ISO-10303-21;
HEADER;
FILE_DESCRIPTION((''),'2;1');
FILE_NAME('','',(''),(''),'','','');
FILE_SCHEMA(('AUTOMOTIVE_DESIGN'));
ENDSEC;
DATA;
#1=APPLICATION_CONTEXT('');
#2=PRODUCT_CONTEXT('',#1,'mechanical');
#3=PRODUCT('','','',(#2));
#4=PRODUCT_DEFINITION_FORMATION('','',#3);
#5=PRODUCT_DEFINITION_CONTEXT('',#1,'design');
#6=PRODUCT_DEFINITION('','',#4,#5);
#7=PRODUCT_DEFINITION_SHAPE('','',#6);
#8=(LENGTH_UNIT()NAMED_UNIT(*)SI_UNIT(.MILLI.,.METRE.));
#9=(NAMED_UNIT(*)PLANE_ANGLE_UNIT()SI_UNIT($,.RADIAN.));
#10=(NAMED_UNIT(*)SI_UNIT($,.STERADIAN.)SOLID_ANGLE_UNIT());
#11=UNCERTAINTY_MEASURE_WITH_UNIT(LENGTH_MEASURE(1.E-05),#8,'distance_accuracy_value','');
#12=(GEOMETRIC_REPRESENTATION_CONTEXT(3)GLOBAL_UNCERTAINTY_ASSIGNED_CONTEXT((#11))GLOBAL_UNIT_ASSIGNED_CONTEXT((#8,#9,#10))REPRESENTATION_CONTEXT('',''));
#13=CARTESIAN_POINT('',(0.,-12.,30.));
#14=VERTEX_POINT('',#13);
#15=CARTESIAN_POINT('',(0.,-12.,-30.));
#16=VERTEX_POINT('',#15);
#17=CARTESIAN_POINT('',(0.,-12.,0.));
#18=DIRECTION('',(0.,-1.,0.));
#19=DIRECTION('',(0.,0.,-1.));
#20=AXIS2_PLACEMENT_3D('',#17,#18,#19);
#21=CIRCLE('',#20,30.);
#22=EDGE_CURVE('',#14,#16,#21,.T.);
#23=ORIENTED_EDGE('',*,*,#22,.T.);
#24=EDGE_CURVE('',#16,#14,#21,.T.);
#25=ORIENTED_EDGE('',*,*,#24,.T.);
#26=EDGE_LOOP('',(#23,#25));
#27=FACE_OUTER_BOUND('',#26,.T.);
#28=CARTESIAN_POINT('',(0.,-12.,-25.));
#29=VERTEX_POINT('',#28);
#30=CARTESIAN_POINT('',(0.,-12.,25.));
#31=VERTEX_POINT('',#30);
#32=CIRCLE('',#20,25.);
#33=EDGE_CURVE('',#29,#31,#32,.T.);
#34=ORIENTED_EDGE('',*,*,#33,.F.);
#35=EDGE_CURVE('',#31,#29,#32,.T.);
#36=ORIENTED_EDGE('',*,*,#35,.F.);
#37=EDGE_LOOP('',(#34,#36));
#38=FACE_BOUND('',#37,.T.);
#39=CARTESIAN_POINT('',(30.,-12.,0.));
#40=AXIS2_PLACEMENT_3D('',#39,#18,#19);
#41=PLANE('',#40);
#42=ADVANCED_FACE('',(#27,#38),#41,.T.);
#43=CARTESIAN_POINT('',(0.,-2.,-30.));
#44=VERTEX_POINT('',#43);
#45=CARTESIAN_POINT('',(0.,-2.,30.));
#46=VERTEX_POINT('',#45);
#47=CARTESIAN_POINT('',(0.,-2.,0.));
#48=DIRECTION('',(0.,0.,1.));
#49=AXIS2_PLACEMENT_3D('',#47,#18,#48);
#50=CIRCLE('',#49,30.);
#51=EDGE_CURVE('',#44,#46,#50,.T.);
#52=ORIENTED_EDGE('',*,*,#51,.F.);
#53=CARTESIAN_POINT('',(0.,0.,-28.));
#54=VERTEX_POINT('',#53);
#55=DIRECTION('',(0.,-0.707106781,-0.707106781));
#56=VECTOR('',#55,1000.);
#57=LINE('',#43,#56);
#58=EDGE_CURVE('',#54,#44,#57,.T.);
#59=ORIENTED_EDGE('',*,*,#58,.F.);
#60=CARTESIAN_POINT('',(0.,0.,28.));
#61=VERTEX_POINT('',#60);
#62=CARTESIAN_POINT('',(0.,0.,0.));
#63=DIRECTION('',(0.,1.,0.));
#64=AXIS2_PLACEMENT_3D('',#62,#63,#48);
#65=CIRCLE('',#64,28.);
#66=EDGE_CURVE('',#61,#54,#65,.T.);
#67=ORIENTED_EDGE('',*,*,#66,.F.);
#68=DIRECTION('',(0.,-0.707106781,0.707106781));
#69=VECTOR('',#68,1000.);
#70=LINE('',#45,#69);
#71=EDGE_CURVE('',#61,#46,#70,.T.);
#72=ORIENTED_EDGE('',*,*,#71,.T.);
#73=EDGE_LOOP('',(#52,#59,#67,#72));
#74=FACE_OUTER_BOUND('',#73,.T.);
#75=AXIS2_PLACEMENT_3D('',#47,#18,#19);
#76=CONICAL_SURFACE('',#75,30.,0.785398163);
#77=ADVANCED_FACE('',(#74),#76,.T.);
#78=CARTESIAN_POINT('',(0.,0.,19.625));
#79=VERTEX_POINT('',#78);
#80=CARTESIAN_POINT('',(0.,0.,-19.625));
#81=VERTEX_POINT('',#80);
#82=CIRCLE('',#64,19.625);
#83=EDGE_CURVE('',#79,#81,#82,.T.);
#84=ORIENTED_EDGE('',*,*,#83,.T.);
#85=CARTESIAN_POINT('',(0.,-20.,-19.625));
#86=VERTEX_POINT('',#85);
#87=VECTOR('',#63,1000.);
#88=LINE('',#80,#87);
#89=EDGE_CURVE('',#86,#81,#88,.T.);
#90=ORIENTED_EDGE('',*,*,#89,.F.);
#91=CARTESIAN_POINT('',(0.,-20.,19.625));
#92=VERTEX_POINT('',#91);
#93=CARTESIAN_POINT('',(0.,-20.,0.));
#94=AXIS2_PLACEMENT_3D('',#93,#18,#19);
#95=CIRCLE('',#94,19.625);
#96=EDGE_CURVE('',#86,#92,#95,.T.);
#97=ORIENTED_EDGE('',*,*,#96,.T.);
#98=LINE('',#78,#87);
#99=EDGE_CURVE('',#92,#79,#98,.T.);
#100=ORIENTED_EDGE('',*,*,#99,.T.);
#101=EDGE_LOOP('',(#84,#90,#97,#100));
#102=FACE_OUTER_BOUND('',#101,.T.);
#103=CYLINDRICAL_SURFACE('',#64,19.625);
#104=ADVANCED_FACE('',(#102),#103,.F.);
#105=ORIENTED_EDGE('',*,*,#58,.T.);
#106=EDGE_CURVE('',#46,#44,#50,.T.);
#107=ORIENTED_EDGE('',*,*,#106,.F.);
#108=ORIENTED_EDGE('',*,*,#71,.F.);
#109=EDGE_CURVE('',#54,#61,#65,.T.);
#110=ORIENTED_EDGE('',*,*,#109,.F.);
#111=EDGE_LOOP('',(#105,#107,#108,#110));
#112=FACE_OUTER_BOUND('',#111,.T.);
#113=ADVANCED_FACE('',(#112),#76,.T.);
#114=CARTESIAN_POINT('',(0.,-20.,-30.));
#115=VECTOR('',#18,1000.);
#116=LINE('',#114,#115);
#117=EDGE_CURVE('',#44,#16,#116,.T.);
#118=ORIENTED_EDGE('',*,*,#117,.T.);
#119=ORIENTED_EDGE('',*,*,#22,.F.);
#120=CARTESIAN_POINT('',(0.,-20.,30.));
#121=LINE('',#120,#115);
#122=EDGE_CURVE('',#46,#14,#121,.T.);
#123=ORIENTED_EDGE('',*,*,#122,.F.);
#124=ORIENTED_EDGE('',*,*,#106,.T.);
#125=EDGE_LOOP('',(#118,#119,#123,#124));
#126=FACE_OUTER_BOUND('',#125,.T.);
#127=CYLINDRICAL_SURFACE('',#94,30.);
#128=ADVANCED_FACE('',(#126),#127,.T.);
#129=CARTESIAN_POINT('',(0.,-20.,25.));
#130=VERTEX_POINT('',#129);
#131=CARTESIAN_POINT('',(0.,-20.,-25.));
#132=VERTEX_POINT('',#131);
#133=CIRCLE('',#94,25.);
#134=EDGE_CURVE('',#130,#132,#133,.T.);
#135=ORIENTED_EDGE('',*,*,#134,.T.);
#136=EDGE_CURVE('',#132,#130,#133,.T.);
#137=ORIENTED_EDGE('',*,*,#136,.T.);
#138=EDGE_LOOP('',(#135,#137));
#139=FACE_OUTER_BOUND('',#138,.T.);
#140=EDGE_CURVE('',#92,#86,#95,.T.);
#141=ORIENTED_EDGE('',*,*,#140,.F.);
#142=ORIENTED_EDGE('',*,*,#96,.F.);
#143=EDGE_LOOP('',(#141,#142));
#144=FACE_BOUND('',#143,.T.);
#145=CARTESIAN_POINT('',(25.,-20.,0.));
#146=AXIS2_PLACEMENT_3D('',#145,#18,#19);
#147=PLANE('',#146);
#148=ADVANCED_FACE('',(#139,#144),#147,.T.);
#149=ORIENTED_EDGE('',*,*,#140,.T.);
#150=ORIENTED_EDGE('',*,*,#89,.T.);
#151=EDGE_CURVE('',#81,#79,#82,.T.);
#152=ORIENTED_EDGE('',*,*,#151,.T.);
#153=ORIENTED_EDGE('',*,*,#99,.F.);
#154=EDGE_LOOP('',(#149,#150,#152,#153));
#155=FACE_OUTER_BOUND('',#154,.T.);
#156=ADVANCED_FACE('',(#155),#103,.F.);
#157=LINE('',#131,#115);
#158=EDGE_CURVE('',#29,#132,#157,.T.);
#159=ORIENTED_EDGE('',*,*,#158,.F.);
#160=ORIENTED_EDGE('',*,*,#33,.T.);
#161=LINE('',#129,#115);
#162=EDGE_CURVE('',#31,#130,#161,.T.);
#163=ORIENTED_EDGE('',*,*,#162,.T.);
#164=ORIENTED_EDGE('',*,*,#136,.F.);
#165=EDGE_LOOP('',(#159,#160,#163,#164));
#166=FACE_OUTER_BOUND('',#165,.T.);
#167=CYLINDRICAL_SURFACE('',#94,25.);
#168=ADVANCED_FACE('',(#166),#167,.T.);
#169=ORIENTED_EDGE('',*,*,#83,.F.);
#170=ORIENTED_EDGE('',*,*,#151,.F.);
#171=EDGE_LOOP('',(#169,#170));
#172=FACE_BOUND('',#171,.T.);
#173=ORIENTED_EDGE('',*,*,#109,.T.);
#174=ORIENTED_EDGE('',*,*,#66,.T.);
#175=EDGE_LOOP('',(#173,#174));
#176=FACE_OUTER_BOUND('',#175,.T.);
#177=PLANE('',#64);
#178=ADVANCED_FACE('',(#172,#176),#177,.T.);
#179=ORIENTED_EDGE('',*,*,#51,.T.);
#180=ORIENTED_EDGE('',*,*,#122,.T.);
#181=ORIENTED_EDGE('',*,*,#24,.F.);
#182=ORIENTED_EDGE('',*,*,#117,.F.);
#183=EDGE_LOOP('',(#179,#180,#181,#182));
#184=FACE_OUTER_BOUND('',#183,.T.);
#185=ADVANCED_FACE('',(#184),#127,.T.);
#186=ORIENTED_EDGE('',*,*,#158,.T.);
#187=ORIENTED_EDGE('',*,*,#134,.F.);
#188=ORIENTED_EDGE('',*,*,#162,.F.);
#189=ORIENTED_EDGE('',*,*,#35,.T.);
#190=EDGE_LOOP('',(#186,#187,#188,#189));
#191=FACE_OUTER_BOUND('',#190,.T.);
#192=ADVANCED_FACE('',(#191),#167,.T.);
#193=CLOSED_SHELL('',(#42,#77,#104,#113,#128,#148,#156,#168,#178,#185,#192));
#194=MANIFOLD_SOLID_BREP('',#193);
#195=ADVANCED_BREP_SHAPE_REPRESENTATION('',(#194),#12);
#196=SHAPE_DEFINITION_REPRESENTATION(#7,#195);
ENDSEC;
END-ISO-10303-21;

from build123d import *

# Parameters (mm, degrees)
G1_1_4_TAPPED_HOLE1_D     = 39.25
G1_1_4_TAPPED_HOLE1_DEPTH = 90.75
G1_1_4_TAPPED_HOLE1_TIP   = 11.791889648
CHAMFER1_SIZE             = 2


with BuildPart() as part:
    # Sketch1 → Revolve1 (revolve)
    with BuildSketch(Plane.XY, mode=Mode.PRIVATE) as revolve1_sk:
        Polygon((0, 0), (30, 0), (30, -12), (25, -12), (25, -20), (0, -20), align=None)
    revolve(revolve1_sk.sketch.rotate(Axis((0, -20, 0), (0, 1, 0)), 90), axis=Axis((0, -20, 0), (0, 1, 0)))

    # G1-1/4 Tapped Hole1
    with Locations(Plane(origin=(0, 0, 0), x_dir=(1, 0, 0), z_dir=(0, 1, 0))):
        with Locations((0, 0)):
            Hole(G1_1_4_TAPPED_HOLE1_D / 2, depth=G1_1_4_TAPPED_HOLE1_DEPTH)
            with Locations((0, 0, -(G1_1_4_TAPPED_HOLE1_DEPTH + G1_1_4_TAPPED_HOLE1_TIP / 2))):  # 118° drill point
                Cone(0, G1_1_4_TAPPED_HOLE1_D / 2, G1_1_4_TAPPED_HOLE1_TIP, mode=Mode.SUBTRACT)

    # Chamfer1
    chamfer1_edges = [part.edges().sort_by_distance(p)[0] for p in [
        (0, 0, 30),
    ]]
    chamfer(chamfer1_edges, length=CHAMFER1_SIZE)


solid = part.part
